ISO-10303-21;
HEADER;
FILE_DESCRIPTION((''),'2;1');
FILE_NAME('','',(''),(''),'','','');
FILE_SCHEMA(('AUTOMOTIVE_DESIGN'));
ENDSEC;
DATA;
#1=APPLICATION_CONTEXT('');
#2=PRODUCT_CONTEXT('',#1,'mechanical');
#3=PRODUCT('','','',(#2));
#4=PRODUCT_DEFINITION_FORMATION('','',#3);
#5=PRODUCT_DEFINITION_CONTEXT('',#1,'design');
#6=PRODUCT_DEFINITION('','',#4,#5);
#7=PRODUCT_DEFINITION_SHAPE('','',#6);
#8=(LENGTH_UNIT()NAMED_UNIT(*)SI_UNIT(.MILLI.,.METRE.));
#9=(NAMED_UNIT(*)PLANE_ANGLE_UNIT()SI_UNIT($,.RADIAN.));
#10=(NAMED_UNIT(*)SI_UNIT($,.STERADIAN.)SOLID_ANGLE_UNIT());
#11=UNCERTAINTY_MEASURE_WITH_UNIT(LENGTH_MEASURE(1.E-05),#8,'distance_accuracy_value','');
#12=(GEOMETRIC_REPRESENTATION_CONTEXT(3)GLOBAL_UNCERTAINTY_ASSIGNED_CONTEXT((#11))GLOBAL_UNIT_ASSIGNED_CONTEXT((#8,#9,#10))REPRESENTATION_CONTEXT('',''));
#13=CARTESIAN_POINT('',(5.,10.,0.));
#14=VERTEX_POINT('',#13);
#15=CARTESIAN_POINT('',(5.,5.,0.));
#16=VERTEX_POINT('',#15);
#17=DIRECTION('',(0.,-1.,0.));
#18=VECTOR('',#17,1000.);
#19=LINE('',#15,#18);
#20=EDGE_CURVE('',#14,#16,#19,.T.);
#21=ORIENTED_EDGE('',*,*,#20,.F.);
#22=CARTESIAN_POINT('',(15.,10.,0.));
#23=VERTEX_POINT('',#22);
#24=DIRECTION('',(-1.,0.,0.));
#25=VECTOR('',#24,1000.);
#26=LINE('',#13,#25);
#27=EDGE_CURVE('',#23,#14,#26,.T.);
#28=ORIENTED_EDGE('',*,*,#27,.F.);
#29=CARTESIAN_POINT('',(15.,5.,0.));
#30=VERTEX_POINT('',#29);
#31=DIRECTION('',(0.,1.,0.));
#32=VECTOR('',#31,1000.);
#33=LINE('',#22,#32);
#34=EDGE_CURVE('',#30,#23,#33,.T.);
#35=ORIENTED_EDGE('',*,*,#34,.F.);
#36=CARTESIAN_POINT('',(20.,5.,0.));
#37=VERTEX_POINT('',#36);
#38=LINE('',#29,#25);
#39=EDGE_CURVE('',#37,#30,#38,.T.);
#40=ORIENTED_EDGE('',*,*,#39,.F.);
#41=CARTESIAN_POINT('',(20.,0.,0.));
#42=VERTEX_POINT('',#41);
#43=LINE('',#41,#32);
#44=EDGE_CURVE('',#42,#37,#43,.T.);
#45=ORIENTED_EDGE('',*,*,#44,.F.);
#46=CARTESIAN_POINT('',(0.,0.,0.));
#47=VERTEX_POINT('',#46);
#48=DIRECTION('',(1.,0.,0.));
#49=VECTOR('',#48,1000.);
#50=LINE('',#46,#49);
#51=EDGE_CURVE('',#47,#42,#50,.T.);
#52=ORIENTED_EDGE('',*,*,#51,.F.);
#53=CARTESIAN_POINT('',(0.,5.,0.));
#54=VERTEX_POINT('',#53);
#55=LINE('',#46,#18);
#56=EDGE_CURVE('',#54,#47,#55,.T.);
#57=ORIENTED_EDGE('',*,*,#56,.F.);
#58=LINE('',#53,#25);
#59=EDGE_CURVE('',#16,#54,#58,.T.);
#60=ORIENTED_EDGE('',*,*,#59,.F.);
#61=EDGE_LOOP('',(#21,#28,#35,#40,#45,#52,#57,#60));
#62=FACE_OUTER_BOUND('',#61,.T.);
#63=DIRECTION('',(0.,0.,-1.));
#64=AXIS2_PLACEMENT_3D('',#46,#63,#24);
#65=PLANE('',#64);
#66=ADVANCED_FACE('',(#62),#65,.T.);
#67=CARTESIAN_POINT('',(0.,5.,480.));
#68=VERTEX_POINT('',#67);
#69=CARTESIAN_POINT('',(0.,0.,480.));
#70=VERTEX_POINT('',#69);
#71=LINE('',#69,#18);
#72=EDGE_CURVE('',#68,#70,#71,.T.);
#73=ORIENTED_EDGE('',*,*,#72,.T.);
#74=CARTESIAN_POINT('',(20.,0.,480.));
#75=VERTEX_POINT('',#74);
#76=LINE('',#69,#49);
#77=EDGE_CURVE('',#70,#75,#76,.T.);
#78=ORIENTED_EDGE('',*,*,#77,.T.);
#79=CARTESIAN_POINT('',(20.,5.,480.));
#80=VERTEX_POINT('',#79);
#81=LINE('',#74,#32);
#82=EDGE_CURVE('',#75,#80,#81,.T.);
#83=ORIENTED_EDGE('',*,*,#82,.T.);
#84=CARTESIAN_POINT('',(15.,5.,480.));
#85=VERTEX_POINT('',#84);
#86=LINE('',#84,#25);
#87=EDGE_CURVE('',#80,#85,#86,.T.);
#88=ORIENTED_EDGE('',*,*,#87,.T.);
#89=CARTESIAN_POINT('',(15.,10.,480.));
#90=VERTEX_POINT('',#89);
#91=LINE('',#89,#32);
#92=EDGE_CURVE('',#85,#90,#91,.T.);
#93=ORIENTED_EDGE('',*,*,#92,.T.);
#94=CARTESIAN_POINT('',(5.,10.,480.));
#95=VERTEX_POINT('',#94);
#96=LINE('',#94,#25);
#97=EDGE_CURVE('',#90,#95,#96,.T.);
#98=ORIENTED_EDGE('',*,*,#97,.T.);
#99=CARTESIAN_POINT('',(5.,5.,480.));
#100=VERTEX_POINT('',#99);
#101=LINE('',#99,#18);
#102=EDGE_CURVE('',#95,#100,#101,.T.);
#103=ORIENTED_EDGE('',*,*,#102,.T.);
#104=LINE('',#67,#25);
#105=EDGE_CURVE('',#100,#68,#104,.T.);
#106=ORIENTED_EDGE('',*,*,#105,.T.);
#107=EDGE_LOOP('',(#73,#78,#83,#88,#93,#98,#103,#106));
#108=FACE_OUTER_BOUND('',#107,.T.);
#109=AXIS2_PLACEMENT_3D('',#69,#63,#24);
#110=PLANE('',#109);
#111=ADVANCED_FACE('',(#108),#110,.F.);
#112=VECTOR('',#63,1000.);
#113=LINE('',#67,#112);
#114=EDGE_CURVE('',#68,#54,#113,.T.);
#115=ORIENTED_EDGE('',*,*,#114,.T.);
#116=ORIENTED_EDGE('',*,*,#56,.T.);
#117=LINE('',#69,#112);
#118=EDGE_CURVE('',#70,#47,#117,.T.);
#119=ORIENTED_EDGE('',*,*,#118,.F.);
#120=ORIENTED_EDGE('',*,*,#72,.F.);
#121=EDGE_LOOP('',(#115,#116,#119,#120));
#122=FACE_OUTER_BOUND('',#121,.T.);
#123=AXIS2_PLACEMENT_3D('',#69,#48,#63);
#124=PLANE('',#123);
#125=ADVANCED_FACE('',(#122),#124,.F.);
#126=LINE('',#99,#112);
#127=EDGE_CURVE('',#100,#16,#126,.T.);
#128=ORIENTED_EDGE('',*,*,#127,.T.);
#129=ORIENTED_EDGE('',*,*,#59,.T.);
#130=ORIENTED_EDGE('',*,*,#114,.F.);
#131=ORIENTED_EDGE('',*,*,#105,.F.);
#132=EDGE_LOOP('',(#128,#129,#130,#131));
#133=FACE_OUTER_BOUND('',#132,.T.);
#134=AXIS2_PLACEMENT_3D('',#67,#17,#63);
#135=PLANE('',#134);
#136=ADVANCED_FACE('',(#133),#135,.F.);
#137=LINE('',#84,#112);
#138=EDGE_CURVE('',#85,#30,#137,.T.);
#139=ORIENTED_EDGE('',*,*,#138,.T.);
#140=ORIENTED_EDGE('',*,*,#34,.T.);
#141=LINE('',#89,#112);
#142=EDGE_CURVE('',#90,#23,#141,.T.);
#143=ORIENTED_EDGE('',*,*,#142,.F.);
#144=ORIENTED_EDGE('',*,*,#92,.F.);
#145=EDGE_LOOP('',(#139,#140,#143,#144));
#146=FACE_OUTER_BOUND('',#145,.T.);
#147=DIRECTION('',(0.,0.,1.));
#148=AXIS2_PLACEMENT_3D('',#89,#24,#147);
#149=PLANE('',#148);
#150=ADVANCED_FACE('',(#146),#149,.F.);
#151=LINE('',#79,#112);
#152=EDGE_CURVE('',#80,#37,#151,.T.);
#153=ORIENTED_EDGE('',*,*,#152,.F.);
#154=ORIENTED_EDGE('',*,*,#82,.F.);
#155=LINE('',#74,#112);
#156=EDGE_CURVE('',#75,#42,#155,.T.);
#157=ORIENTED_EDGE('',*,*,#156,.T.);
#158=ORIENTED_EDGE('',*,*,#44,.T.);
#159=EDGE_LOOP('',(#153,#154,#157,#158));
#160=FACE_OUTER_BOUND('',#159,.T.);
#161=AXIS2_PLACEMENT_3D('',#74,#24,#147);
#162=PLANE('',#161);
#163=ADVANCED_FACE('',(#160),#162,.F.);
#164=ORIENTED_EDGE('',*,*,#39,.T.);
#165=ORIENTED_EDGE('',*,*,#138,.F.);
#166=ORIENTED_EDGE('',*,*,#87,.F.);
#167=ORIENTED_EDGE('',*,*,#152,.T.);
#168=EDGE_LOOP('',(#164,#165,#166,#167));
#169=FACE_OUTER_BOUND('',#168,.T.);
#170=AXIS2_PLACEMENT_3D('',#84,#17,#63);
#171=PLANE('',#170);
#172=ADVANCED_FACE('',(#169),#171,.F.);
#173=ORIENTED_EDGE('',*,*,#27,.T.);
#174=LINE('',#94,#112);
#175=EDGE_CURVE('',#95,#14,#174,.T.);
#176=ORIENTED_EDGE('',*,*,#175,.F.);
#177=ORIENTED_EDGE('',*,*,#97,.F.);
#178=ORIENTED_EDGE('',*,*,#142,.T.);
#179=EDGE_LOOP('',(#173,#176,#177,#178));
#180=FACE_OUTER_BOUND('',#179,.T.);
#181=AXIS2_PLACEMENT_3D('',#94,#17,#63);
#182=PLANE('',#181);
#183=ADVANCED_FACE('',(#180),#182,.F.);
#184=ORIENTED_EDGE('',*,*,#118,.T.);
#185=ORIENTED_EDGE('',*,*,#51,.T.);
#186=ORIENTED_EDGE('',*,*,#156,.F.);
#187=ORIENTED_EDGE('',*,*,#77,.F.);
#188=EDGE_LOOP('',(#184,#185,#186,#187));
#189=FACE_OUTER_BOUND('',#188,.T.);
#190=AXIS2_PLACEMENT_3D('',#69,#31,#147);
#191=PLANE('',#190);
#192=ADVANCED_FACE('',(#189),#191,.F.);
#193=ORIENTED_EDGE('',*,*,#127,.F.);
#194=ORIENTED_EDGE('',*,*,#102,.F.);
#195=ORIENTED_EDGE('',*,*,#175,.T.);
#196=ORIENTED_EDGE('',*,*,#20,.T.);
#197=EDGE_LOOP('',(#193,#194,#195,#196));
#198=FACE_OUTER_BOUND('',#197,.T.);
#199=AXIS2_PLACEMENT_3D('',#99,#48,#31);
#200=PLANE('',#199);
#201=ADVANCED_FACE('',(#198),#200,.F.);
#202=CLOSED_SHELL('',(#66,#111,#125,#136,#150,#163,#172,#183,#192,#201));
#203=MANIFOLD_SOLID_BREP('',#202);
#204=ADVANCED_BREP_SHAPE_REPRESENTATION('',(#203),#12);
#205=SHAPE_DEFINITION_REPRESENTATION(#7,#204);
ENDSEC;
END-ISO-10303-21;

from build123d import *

# Parameters (mm, degrees)
BOSS_EXTRUDE1_DEPTH = 480


with BuildPart() as part:
    # Sketch1 → Boss-Extrude1 (new body)
    with BuildSketch(Plane.XY):
        Polygon((5, 5), (5, 10), (15, 10), (15, 5), (20, 5), (20, 0), (0, 0), (0, 5), align=None)
    extrude(amount=BOSS_EXTRUDE1_DEPTH)


solid = part.part
